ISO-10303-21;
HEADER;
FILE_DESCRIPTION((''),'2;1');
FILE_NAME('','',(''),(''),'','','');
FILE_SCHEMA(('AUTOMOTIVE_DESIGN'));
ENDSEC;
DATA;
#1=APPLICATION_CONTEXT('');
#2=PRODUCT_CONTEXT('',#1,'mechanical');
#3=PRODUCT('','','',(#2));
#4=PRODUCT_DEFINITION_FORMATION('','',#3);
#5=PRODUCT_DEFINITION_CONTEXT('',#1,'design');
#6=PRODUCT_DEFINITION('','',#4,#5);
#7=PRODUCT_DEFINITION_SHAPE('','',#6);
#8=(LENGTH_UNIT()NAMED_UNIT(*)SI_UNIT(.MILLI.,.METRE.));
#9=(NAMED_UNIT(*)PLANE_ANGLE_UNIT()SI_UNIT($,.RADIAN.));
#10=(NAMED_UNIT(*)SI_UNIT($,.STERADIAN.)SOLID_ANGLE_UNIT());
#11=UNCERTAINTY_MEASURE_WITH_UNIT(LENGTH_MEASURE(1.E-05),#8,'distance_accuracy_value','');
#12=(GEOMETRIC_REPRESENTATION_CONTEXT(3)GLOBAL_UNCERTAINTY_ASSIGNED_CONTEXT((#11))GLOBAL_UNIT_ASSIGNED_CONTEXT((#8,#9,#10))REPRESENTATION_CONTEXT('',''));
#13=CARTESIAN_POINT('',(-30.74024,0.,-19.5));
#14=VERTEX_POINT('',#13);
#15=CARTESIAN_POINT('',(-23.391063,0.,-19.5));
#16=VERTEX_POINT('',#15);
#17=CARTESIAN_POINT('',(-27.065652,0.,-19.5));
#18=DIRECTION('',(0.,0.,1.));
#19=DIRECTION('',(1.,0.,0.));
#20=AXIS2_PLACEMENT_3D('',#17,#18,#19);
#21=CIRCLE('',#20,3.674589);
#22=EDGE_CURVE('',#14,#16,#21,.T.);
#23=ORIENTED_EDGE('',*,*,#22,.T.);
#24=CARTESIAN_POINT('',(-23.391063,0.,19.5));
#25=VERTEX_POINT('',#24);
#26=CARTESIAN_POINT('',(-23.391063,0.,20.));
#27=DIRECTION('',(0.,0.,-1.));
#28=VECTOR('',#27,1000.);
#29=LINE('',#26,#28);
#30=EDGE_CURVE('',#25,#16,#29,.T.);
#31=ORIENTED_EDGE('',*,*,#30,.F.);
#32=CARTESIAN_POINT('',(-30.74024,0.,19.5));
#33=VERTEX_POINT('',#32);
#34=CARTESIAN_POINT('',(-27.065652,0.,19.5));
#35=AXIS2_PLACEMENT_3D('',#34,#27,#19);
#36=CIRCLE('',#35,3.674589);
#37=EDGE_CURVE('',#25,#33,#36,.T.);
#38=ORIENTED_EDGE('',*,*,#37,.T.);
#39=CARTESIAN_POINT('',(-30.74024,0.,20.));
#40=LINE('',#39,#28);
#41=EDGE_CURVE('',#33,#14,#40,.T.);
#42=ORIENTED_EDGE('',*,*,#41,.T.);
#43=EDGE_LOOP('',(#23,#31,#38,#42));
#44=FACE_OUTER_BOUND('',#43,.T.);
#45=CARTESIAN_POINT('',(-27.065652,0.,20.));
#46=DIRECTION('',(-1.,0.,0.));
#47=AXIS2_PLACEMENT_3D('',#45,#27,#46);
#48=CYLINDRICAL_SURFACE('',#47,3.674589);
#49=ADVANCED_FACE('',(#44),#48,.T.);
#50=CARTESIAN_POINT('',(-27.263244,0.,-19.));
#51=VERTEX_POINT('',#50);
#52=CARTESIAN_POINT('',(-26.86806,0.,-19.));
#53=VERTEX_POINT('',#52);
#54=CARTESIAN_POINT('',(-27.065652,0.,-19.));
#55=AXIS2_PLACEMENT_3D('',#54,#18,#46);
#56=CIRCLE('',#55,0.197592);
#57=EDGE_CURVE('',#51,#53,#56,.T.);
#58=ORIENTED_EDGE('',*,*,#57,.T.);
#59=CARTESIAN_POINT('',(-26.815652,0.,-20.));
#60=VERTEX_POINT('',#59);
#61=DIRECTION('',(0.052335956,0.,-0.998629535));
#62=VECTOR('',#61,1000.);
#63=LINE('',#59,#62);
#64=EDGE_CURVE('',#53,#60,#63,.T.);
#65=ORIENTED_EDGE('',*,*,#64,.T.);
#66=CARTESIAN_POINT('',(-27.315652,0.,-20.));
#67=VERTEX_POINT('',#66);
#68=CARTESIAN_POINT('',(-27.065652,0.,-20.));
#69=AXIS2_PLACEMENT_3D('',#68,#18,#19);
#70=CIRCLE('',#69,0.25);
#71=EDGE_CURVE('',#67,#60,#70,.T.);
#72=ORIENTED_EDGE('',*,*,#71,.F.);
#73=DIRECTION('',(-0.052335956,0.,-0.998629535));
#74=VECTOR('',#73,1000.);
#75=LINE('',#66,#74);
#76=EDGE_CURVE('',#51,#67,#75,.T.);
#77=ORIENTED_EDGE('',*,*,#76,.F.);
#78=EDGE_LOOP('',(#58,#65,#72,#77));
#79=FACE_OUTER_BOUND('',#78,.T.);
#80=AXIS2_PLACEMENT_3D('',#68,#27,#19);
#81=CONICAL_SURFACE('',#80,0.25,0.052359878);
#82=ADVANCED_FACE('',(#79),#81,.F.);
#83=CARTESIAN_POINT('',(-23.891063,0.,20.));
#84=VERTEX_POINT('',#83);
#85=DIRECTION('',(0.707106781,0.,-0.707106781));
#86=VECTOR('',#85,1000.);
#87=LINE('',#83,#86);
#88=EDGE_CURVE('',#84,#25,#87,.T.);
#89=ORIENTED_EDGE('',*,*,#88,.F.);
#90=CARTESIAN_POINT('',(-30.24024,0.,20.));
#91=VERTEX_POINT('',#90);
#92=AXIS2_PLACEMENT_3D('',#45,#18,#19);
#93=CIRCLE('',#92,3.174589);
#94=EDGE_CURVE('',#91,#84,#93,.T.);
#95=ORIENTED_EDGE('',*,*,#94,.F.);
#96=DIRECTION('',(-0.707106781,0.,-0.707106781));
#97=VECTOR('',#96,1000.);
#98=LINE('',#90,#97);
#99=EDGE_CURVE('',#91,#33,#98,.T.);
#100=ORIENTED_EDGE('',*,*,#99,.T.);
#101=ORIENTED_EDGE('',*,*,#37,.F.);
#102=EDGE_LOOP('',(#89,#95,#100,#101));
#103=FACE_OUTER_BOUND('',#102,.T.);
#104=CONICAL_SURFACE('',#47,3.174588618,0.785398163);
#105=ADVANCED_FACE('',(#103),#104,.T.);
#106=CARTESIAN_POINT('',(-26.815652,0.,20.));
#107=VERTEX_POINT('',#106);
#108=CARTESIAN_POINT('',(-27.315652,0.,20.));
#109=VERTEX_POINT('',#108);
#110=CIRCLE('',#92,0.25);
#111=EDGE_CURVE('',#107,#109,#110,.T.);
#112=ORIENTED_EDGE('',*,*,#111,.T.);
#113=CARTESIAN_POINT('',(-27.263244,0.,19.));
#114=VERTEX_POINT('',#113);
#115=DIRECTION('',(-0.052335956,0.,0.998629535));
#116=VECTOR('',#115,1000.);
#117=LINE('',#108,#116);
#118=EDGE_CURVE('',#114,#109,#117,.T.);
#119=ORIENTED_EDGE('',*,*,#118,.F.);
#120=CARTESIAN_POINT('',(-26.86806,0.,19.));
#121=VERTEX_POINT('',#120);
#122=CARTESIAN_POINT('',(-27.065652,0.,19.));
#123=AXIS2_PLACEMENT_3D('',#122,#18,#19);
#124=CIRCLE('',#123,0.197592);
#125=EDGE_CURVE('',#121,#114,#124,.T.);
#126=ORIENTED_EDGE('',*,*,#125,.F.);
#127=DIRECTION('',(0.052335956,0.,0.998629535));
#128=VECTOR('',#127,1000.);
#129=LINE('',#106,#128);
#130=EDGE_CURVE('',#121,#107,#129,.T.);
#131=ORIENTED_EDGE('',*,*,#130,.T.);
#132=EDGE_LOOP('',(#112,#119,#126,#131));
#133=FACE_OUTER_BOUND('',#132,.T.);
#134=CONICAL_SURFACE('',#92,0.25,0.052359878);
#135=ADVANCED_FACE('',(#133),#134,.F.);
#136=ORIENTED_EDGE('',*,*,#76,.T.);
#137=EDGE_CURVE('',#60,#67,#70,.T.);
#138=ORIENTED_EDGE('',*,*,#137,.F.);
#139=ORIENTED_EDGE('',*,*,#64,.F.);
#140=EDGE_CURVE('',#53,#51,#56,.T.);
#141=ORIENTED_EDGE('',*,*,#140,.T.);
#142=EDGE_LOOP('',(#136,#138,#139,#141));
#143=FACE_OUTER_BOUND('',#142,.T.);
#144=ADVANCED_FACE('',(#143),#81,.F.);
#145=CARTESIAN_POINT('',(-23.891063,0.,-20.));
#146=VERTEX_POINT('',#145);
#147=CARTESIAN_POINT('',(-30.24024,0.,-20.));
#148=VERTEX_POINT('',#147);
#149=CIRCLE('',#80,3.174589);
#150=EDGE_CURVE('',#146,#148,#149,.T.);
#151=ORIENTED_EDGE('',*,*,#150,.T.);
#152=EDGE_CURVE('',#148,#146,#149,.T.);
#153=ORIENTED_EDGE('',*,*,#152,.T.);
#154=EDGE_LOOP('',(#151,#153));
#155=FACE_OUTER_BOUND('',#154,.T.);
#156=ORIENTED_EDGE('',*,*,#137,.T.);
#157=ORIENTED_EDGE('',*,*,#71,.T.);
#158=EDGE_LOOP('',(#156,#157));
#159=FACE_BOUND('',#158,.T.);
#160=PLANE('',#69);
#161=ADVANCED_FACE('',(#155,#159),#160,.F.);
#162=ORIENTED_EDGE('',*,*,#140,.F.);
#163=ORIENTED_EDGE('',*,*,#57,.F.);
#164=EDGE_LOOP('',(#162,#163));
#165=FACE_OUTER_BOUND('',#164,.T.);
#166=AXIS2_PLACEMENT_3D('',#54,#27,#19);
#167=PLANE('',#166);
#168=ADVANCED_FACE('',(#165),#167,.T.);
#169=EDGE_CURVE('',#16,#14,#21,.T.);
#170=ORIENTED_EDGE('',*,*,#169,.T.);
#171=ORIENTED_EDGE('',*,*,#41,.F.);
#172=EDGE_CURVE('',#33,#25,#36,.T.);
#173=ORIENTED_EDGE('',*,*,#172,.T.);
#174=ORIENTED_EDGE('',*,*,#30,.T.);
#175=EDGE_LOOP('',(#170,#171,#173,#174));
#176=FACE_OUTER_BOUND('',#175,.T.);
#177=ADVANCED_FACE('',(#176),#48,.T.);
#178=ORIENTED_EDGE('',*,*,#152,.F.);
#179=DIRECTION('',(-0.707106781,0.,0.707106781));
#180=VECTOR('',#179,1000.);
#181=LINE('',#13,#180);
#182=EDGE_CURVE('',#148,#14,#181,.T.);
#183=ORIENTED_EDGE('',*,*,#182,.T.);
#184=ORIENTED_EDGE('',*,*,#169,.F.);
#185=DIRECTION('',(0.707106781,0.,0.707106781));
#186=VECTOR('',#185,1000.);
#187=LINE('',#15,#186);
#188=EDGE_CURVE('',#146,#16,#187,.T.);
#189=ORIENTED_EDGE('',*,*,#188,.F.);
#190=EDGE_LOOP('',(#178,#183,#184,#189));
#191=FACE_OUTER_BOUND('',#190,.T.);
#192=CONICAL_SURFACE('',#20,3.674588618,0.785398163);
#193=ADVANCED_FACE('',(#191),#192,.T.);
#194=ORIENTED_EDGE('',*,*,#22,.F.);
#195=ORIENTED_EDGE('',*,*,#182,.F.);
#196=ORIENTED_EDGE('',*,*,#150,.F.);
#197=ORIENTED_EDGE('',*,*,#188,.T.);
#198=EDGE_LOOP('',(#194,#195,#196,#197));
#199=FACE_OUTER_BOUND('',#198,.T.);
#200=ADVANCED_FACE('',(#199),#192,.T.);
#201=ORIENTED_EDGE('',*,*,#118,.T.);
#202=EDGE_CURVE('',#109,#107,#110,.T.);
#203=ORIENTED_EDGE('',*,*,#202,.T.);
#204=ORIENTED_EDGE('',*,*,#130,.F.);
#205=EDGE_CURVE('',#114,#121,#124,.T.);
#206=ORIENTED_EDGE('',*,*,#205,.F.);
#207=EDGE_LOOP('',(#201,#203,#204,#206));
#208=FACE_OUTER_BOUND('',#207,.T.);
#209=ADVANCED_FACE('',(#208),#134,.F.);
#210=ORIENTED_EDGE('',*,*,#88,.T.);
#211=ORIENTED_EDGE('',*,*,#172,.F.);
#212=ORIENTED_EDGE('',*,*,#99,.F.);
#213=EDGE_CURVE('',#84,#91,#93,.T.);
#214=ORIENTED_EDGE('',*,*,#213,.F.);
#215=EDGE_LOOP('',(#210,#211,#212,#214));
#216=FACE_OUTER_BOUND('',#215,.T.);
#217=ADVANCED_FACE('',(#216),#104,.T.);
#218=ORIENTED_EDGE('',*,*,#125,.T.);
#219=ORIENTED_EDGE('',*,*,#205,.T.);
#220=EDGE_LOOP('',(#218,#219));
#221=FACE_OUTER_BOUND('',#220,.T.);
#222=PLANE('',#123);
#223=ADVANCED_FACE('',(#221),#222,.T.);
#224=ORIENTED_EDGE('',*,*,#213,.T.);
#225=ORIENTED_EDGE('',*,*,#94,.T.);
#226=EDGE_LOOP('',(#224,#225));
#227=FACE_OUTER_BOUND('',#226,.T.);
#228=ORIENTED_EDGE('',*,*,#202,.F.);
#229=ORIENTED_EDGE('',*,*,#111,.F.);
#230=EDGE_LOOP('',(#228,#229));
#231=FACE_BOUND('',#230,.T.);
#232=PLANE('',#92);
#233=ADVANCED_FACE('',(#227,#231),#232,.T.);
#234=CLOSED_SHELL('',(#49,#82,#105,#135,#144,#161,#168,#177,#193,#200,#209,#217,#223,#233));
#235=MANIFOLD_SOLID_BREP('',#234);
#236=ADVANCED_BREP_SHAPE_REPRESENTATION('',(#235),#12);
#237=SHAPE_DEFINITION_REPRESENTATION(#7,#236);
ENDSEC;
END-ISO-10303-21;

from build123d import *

# Parameters (mm, degrees)
SKETCH1_R               = 3.674588618
BOSS_EXTRUDE1_DEPTH     = 20
CHAMFER2_SIZE           = 0.5
SKETCH2_R               = 0.25
CUT_EXTRUDE1_DEPTH      = 1
CUT_EXTRUDE1_DRAFT      = -3
MIRROR1_COPY_1_SKETCH_R = 0.25
MIRROR1_COPY_1_DEPTH    = 1
MIRROR1_COPY_1_DRAFT    = -3


with BuildPart() as part:
    # Sketch1 → Boss-Extrude1 (new, symmetric)
    with BuildSketch(Plane.XY):
        with Locations(Location((-27.065651732, 0, 0), (0, 0, 180))):
            Circle(SKETCH1_R)
    extrude(amount=BOSS_EXTRUDE1_DEPTH, both=True)

    # Chamfer2
    chamfer2_edges = [part.edges().sort_by_distance(p)[0] for p in [
        (-23.391063114, 0, -20),
        (-23.391063114, 0, 20),
    ]]
    chamfer(chamfer2_edges, length=CHAMFER2_SIZE)


with BuildPart() as cut_extrude1_tool:
    # Sketch2 → Cut-Extrude1 (with draft: the straight prism first)
    with BuildSketch(Plane.XY.offset(20)):
        with Locations((-27.065651732, 0)):
            Circle(SKETCH2_R)
    extrude(amount=-CUT_EXTRUDE1_DEPTH)
    # Cut-Extrude1: the draft: its side faces are tilted about the plane it starts from
    cut_extrude1_sides = [cut_extrude1_tool.faces().sort_by_distance(p)[0] for p in [
        (-27.315651732, 0, 19.5),
    ]]
    draft(cut_extrude1_sides, Plane.XY.offset(20), CUT_EXTRUDE1_DRAFT)


with BuildPart() as part_1:
    add(part.part)

    # Cut-Extrude1: cut by cut_extrude1_tool
    add(cut_extrude1_tool.part, mode=Mode.SUBTRACT)


with BuildPart() as mirror1_copy_1_tool:
    # Mirror1 copy 1 sketch → Mirror1 copy 1 (with draft: the straight prism first)
    with BuildSketch(Plane(origin=(0, 0, -20), x_dir=(1, 0, 0), z_dir=(0, 0, -1))):
        with Locations((-27.065651732, 0)):
            Circle(MIRROR1_COPY_1_SKETCH_R)
    extrude(amount=-MIRROR1_COPY_1_DEPTH)
    # Mirror1 copy 1: the draft: its side faces are tilted about the plane it starts from
    mirror1_copy_1_sides = [mirror1_copy_1_tool.faces().sort_by_distance(p)[0] for p in [
        (-27.315651732, 0, -19.5),
    ]]
    draft(mirror1_copy_1_sides, Plane(origin=(0, 0, -20), x_dir=(1, 0, 0), z_dir=(0, 0, -1)), MIRROR1_COPY_1_DRAFT)


with BuildPart() as part_2:
    add(part_1.part)

    # Mirror1 copy 1: cut by mirror1_copy_1_tool
    add(mirror1_copy_1_tool.part, mode=Mode.SUBTRACT)


solid = part_2.part
